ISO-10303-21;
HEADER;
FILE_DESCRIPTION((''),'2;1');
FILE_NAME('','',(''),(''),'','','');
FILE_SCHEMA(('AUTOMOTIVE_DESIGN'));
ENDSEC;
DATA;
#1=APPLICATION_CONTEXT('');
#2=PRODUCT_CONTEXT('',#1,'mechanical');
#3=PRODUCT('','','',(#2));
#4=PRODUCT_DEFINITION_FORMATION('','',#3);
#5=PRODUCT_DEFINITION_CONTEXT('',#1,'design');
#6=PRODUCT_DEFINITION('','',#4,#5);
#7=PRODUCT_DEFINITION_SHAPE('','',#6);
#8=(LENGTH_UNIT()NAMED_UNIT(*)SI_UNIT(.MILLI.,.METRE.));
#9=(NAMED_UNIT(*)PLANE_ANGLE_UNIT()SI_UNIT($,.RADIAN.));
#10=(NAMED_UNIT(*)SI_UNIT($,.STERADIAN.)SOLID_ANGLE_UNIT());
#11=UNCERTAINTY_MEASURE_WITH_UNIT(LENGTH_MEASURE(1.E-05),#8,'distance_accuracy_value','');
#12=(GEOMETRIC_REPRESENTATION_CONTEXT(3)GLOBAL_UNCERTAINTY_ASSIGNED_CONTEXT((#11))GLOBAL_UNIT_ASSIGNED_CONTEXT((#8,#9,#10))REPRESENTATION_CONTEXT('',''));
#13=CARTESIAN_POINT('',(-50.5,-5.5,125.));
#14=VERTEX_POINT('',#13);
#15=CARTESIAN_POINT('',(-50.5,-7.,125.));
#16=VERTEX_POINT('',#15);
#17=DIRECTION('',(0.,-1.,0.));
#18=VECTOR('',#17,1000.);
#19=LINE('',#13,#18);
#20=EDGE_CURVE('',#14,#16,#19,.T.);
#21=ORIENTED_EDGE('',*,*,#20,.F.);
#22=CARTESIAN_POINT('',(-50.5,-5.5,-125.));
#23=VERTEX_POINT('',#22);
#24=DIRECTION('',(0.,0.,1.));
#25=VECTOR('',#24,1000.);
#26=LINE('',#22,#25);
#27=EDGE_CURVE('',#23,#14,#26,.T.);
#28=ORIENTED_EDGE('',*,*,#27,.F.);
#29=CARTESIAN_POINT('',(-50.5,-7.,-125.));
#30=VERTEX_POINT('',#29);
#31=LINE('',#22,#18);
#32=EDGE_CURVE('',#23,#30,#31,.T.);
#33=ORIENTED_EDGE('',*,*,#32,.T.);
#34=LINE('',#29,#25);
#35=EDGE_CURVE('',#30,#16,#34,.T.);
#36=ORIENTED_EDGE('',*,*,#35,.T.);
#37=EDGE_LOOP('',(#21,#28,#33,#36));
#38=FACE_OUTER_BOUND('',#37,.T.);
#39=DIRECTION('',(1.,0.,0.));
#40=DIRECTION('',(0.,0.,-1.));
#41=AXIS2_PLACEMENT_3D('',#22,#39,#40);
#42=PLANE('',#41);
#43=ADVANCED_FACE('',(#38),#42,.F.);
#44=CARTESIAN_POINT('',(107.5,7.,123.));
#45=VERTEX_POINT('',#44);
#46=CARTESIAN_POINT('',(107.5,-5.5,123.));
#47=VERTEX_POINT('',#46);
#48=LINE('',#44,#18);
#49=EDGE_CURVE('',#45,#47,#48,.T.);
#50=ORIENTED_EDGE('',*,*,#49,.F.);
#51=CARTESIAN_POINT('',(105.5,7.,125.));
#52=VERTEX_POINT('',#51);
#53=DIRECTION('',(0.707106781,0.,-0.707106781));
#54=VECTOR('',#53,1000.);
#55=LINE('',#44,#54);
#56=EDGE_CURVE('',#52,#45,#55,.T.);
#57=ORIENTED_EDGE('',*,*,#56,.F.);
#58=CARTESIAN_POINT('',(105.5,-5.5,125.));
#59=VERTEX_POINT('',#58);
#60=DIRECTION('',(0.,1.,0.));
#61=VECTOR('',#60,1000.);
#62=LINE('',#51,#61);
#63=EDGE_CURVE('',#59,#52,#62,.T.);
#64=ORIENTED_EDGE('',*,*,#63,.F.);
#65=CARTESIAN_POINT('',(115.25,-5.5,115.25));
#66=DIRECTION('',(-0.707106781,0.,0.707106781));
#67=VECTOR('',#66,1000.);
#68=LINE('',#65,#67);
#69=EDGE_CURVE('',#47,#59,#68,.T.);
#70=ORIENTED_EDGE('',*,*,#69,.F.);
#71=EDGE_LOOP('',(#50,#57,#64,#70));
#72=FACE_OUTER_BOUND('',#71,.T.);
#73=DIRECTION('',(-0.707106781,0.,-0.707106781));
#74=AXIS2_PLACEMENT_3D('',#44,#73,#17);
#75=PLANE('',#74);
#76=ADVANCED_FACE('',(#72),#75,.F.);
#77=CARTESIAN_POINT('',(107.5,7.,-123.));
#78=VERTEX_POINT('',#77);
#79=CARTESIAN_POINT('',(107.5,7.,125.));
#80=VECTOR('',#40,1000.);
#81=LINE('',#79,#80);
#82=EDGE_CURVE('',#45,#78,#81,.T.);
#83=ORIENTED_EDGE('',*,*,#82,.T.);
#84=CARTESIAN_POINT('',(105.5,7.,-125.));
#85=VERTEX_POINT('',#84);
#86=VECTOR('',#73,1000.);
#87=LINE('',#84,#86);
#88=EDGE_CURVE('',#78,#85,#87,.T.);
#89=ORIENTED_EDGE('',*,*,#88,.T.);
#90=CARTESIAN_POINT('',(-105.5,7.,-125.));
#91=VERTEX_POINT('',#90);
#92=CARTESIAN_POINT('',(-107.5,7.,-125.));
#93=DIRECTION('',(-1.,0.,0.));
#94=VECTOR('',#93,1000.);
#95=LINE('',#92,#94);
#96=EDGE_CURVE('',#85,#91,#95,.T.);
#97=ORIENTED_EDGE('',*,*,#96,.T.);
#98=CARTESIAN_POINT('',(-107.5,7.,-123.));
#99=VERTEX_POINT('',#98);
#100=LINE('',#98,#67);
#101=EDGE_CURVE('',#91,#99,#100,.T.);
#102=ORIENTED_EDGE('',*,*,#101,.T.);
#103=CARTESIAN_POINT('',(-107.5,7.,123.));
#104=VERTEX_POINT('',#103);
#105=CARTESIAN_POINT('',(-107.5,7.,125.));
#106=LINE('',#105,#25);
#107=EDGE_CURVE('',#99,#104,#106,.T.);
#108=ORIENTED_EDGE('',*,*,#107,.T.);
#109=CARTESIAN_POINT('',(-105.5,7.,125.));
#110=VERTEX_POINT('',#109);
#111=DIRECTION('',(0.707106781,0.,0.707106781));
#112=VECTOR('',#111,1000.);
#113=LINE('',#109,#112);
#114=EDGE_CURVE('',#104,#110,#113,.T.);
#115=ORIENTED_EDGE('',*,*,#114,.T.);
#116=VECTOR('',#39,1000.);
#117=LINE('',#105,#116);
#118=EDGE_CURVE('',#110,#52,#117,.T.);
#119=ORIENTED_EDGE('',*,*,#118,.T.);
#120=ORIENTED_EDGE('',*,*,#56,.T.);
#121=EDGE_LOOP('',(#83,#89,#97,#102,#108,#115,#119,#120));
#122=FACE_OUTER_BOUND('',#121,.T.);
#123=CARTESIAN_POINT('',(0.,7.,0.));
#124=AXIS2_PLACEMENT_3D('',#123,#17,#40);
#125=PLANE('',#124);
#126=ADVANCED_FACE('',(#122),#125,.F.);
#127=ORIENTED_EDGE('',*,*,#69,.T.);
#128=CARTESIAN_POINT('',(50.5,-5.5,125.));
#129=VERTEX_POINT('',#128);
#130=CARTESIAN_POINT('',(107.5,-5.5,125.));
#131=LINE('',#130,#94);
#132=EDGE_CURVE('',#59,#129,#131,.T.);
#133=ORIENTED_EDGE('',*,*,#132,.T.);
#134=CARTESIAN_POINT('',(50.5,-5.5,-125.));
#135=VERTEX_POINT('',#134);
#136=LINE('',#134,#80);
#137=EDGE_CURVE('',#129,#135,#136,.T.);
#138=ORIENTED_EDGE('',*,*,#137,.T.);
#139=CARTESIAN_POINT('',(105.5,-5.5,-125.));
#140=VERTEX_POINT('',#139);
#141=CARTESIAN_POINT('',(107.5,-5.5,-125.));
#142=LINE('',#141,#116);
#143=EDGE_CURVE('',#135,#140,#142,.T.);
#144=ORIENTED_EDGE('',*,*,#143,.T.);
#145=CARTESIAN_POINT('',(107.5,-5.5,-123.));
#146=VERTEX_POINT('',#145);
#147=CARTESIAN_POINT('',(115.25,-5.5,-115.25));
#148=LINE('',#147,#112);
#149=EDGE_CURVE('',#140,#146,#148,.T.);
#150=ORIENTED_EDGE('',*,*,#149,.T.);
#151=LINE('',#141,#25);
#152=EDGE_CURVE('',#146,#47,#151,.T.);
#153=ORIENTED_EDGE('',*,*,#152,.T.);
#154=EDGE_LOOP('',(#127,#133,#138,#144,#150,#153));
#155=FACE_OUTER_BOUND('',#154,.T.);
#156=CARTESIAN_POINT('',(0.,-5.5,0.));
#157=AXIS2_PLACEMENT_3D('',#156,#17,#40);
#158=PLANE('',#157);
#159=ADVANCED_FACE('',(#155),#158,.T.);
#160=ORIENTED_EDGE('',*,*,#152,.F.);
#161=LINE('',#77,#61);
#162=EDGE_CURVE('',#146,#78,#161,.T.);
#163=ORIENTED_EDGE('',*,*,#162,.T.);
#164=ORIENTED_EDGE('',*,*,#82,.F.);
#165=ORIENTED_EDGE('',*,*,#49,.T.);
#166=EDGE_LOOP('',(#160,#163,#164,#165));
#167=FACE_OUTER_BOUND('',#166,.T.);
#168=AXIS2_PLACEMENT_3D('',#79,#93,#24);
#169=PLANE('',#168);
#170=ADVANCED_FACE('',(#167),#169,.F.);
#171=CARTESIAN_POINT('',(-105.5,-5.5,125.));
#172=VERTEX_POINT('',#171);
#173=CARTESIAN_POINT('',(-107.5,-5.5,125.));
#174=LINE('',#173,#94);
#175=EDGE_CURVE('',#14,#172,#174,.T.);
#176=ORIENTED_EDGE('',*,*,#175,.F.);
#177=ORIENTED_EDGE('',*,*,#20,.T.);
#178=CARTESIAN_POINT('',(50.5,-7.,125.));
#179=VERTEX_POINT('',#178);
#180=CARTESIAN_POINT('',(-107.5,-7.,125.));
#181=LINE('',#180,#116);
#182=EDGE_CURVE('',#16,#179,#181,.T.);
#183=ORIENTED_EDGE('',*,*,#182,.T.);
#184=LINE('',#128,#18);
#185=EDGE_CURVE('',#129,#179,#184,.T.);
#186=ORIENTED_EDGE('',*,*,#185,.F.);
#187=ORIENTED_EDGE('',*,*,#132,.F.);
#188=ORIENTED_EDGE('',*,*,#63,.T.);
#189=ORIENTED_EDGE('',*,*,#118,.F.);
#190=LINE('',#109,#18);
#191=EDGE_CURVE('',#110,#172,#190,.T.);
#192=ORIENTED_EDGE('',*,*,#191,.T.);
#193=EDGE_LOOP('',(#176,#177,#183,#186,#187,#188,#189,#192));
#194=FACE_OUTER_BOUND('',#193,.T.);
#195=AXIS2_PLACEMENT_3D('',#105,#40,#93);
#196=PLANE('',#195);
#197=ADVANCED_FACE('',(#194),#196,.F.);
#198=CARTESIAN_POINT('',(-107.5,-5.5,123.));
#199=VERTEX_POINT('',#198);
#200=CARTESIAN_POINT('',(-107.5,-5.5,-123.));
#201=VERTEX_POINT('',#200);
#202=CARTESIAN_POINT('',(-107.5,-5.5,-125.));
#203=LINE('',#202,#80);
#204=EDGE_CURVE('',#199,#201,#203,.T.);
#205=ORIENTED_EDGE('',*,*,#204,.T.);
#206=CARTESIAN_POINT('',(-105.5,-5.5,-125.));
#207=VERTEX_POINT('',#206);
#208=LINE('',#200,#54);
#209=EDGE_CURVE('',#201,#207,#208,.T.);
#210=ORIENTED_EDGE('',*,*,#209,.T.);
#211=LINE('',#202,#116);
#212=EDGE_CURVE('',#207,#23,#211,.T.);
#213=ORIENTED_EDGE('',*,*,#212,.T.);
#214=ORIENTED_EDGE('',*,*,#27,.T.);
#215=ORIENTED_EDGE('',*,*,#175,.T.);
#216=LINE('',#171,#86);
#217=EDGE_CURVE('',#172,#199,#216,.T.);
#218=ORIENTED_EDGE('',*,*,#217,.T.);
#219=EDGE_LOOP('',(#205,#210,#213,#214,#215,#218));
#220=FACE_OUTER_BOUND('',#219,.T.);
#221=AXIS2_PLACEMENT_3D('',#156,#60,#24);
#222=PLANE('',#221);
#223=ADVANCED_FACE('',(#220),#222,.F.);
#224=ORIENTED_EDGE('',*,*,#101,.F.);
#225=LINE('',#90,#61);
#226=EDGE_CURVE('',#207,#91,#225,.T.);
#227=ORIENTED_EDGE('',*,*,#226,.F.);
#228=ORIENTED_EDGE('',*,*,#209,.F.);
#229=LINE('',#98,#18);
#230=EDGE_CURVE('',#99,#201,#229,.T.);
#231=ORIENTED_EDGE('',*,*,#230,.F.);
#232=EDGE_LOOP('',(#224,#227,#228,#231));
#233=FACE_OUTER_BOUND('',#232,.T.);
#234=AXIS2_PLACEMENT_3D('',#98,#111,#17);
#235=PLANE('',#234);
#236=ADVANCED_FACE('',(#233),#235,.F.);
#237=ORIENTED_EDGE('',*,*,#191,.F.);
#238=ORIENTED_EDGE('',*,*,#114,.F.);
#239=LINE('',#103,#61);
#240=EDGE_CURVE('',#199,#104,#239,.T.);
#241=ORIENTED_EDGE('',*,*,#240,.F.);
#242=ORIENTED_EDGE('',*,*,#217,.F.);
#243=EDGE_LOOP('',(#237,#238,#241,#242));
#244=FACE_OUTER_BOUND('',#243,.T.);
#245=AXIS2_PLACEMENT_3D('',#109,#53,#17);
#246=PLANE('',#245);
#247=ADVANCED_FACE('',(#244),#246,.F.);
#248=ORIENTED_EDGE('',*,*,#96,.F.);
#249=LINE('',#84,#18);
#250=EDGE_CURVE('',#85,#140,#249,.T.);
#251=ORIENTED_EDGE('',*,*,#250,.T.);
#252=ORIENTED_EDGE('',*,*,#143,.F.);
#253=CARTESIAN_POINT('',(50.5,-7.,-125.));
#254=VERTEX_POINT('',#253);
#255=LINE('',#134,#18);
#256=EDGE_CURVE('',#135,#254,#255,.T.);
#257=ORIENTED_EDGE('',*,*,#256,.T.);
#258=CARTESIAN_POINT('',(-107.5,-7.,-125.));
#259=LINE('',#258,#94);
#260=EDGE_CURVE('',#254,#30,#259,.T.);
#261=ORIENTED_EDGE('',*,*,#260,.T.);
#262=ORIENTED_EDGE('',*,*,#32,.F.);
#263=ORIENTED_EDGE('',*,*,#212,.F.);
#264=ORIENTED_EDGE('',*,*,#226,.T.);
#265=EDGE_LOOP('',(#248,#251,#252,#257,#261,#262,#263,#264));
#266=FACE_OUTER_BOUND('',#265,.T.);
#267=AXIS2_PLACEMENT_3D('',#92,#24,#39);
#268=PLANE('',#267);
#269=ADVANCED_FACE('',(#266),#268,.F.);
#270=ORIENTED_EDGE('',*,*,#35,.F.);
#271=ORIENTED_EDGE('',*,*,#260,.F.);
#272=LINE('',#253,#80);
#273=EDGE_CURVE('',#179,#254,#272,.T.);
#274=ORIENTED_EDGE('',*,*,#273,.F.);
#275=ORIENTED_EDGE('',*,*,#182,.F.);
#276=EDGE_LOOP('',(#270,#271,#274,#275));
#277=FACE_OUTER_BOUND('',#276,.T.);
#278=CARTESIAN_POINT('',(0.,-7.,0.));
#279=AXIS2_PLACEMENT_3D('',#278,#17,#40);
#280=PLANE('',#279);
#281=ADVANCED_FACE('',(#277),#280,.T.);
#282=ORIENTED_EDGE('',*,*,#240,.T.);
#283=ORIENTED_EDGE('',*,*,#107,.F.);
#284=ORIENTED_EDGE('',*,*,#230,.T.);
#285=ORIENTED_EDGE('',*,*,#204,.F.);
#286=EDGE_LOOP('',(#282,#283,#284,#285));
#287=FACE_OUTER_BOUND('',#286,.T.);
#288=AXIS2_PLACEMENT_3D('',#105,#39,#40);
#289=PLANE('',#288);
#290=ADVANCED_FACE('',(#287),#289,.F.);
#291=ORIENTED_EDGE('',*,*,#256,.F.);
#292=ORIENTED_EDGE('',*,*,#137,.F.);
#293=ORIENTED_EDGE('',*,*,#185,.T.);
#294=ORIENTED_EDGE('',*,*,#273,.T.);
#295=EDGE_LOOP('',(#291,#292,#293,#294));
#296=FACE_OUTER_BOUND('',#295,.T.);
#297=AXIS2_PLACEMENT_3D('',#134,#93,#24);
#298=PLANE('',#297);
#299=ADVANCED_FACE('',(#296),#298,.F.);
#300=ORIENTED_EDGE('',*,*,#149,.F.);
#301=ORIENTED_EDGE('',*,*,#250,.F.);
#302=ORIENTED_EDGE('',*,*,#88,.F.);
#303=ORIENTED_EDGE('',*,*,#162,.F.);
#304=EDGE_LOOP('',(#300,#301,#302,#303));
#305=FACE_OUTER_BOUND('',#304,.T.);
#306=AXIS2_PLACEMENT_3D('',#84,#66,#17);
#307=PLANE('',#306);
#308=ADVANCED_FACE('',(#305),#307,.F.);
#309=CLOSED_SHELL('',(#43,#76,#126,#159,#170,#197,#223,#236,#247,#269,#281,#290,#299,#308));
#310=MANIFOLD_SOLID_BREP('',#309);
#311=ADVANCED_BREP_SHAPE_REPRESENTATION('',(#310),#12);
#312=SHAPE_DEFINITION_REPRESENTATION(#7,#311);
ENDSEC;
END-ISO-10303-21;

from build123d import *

# Parameters (mm, degrees)
SKETCH_1_W          = 215
SKETCH_1_H          = 250
EXTRUDE_1_DEPTH     = 7
SKETCH_2_W          = 57
SKETCH_2_H          = 250
CUT_EXTRUDE_1_DEPTH = 1.5
CHAMFER_1_SIZE      = 2


with BuildPart() as part:
    # 草图1 → 凸台-拉伸1 (new, symmetric)
    with BuildSketch(Plane(origin=(0, 0, 0), x_dir=(1, 0, 0), z_dir=(0, 1, 0))):
        Rectangle(SKETCH_1_W, SKETCH_1_H)
    extrude(amount=EXTRUDE_1_DEPTH, both=True)

    # 草图2 → 切除-拉伸1 (cut)
    with BuildSketch(Plane.XZ.offset(7)):
        with Locations((79, 0)):
            Rectangle(SKETCH_2_W, SKETCH_2_H)
        with Locations((-79, 0)):
            Rectangle(SKETCH_2_W, SKETCH_2_H)
    extrude(amount=-CUT_EXTRUDE_1_DEPTH, mode=Mode.SUBTRACT)

    # 倒角1
    chamfer_1_edges = [part.edges().sort_by_distance(p)[0] for p in [
        (107.5, 0.75, 125),
        (-107.5, 0.75, 125),
        (-107.5, 0.75, -125),
        (107.5, 0.75, -125),
    ]]
    chamfer(chamfer_1_edges, length=CHAMFER_1_SIZE)


solid = part.part
